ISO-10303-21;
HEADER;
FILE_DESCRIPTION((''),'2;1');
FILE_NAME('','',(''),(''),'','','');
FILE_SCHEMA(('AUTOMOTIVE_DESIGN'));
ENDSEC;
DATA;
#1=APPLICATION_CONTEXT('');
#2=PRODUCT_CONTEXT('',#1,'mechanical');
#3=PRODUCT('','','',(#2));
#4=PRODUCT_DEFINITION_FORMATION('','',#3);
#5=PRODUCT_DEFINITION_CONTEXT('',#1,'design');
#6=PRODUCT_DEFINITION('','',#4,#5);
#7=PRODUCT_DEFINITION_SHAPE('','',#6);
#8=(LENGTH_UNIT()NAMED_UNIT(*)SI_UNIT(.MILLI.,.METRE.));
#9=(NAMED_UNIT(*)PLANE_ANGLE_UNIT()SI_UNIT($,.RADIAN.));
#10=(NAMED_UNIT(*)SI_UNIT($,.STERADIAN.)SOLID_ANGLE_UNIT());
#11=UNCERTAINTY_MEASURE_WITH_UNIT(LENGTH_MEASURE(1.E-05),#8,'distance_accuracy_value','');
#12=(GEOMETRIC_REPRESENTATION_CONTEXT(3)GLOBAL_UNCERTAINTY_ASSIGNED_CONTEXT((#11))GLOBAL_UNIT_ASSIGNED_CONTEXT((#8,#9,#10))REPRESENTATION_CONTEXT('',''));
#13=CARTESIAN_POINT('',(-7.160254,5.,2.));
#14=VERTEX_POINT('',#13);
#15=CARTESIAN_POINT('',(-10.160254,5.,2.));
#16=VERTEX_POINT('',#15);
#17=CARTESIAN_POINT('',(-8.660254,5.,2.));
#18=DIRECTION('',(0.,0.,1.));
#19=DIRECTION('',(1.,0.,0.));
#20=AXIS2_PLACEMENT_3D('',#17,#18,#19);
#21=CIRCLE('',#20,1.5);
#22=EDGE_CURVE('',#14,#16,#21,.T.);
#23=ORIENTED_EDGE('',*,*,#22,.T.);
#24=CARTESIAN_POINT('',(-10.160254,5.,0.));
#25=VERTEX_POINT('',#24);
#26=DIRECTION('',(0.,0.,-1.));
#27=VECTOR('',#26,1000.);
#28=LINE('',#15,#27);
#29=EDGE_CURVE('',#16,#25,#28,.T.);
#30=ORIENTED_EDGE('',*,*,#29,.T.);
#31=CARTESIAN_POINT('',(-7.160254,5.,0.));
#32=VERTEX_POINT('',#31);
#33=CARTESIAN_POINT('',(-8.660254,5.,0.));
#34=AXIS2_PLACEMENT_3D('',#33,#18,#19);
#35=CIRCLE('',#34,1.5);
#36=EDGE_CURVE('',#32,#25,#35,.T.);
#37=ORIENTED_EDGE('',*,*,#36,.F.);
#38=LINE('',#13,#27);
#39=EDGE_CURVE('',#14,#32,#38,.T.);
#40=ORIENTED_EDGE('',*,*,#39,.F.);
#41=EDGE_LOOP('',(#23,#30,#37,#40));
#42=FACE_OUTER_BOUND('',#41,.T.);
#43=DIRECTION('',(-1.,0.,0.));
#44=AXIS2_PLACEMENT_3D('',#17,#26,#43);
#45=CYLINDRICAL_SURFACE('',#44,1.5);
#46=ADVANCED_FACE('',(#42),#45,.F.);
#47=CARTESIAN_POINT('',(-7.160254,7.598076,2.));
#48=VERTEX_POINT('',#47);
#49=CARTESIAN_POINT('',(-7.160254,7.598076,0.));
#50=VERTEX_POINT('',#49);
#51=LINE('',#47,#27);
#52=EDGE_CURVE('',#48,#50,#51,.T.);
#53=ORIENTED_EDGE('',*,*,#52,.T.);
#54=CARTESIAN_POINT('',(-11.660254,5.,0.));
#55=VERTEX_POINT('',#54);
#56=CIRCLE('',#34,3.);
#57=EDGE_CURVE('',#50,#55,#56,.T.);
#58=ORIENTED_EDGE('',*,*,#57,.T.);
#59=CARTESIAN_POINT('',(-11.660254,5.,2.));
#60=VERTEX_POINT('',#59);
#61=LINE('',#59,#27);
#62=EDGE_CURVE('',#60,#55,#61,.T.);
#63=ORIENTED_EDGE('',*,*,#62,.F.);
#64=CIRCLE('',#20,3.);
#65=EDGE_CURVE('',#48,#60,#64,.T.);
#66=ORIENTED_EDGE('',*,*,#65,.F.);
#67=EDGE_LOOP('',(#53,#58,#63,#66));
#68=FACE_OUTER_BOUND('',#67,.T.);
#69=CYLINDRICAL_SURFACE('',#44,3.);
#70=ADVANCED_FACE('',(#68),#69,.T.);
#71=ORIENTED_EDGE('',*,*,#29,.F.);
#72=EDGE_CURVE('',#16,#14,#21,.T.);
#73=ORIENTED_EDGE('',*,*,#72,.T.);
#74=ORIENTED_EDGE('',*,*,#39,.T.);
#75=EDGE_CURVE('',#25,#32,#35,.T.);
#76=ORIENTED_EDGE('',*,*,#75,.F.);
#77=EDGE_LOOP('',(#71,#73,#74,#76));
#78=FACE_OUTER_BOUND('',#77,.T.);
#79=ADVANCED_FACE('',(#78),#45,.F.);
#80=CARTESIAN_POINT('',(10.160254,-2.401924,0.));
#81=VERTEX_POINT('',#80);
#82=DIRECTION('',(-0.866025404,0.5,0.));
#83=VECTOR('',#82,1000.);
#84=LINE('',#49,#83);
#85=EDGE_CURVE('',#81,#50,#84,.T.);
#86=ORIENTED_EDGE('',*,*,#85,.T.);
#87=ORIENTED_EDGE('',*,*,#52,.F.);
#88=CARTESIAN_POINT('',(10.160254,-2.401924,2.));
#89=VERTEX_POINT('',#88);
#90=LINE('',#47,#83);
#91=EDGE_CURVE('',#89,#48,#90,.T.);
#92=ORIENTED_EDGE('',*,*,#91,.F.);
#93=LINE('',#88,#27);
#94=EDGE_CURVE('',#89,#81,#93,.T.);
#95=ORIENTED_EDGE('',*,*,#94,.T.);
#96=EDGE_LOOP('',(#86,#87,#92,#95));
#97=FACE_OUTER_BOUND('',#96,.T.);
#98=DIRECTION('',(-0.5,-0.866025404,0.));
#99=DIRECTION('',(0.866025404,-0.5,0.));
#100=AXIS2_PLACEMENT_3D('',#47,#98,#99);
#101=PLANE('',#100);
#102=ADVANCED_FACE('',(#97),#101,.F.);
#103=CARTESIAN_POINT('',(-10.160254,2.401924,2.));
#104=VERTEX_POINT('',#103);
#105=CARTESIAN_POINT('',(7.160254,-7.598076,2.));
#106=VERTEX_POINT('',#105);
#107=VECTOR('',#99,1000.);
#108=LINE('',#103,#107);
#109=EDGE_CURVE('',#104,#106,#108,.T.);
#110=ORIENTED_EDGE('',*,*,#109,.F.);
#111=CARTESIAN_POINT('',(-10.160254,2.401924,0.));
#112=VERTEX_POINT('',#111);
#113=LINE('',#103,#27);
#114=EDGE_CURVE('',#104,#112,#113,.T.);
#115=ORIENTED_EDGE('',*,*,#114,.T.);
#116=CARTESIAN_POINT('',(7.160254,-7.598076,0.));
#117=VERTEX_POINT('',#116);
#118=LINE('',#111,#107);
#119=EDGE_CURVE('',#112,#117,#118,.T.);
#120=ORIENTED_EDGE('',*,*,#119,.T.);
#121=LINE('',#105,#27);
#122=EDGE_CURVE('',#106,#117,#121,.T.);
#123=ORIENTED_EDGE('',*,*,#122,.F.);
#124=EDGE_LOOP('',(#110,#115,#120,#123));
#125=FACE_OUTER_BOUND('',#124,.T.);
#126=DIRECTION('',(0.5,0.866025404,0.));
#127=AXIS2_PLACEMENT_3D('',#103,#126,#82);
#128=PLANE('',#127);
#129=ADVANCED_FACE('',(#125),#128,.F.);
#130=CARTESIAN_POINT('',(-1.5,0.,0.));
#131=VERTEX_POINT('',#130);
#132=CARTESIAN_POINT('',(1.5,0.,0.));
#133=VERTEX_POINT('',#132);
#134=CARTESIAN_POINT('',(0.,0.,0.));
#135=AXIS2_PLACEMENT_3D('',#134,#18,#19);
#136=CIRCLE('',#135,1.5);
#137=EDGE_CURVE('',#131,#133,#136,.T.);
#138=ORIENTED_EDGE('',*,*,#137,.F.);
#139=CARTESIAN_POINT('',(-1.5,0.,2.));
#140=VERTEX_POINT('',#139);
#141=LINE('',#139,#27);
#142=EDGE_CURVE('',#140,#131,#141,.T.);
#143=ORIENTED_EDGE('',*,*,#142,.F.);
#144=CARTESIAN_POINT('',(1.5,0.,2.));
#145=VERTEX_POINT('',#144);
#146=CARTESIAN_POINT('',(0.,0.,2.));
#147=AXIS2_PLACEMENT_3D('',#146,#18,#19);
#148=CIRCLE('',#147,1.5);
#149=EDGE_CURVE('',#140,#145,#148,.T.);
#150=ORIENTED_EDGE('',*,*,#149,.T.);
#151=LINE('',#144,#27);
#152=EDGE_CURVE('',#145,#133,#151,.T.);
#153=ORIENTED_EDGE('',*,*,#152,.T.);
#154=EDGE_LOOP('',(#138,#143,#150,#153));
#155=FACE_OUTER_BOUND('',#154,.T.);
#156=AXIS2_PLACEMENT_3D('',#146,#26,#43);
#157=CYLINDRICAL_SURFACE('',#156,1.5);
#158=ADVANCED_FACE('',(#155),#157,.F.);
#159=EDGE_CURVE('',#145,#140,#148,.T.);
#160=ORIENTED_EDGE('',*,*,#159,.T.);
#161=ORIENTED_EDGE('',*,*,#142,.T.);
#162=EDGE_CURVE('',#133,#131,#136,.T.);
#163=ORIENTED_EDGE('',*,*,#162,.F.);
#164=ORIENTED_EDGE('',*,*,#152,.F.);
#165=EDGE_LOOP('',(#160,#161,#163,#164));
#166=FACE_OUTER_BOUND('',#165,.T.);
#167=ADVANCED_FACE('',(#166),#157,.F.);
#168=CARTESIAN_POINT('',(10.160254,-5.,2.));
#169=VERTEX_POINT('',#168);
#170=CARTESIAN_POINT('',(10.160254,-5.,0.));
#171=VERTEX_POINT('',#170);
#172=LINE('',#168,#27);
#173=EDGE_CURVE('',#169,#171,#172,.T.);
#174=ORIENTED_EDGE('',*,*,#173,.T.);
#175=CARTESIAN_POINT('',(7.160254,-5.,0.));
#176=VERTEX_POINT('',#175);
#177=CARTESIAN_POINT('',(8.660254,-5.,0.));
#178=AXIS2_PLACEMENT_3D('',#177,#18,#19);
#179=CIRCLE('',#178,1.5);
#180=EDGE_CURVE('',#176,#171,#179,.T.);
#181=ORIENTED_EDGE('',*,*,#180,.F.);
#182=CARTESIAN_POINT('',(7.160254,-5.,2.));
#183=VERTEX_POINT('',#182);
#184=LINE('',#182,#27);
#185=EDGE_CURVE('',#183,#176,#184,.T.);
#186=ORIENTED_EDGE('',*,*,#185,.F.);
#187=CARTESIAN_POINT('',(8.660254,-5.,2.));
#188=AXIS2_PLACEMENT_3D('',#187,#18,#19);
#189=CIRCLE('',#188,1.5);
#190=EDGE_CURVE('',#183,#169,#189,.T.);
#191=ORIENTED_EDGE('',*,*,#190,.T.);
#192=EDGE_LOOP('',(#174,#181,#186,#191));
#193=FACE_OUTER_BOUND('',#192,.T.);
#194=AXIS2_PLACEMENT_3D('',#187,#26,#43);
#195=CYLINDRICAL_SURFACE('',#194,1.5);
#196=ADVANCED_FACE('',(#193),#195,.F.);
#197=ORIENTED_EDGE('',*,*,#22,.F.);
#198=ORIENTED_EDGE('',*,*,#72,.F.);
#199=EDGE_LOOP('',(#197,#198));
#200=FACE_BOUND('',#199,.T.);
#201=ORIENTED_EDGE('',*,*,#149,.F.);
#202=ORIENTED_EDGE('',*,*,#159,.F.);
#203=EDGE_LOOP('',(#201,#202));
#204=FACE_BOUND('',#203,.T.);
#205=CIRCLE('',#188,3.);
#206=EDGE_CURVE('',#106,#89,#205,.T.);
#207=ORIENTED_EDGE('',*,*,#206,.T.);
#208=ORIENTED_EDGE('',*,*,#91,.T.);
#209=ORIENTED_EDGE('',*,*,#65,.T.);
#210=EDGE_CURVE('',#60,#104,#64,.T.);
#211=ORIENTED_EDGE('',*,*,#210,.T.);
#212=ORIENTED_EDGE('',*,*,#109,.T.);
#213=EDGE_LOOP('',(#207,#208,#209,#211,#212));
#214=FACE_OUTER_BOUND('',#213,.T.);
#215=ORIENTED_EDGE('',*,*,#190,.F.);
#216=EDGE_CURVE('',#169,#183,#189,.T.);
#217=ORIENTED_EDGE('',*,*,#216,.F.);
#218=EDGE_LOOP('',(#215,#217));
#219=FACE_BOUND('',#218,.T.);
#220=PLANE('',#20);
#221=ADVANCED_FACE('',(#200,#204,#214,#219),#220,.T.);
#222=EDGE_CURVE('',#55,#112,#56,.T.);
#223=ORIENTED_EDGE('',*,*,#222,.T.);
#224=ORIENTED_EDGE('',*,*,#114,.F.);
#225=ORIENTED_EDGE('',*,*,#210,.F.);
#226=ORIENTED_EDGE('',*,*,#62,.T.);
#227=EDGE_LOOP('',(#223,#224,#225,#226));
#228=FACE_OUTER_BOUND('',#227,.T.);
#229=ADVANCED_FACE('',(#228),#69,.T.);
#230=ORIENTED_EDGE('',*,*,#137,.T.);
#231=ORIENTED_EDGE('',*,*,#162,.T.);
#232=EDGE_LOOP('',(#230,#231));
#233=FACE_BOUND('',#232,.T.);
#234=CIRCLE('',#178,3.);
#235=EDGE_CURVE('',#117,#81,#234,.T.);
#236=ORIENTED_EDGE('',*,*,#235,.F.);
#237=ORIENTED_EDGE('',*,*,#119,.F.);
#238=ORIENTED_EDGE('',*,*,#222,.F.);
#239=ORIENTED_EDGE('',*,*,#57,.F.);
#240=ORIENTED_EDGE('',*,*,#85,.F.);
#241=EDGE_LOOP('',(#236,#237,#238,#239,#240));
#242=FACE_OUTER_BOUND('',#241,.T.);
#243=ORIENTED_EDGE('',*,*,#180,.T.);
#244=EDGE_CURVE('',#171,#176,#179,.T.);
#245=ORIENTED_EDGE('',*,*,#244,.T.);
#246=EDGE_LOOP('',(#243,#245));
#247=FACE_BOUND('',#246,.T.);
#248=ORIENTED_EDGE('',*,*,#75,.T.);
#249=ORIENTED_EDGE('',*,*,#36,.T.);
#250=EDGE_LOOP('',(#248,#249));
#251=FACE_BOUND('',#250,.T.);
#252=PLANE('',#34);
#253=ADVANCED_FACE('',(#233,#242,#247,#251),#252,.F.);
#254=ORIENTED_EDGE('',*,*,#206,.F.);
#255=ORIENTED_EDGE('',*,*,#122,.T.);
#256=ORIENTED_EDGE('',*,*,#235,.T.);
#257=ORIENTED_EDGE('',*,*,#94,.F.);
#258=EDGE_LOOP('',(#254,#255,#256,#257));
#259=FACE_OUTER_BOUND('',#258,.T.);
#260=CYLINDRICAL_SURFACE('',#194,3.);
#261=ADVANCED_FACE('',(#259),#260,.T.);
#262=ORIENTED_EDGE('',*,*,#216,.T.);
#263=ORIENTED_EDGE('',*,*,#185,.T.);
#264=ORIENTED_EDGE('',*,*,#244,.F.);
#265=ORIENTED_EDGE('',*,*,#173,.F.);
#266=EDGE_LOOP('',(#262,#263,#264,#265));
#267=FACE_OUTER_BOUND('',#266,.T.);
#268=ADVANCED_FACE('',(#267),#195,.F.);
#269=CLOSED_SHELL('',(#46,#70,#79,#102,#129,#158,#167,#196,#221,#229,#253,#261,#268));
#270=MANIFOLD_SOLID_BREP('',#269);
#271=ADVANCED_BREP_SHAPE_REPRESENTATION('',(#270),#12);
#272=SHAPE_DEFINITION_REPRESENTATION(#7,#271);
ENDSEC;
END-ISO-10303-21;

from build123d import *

# Parameters (mm, degrees)
SKETCH1_R           = 1.5
BOSS_EXTRUDE1_DEPTH = 2


with BuildPart() as part:
    # Sketch1 → Boss-Extrude1 (new body)
    with BuildSketch(Plane.XY):
        with BuildLine():
            Line((-10.160254038, 2.401923789), (7.160254038, -7.598076211))
            ThreePointArc((7.160254038, -7.598076211), (11.258330249, -6.5), (10.160254038, -2.401923789))
            Line((10.160254038, -2.401923789), (-7.160254038, 7.598076211))
            ThreePointArc((-7.160254038, 7.598076211), (-11.258330249, 6.5), (-10.160254038, 2.401923789))
        make_face()
        Circle(SKETCH1_R, mode=Mode.SUBTRACT)
        with Locations((8.660254038, -5)):
            Circle(SKETCH1_R, mode=Mode.SUBTRACT)
        with Locations((-8.660254038, 5)):
            Circle(SKETCH1_R, mode=Mode.SUBTRACT)
    extrude(amount=BOSS_EXTRUDE1_DEPTH)


solid = part.part
